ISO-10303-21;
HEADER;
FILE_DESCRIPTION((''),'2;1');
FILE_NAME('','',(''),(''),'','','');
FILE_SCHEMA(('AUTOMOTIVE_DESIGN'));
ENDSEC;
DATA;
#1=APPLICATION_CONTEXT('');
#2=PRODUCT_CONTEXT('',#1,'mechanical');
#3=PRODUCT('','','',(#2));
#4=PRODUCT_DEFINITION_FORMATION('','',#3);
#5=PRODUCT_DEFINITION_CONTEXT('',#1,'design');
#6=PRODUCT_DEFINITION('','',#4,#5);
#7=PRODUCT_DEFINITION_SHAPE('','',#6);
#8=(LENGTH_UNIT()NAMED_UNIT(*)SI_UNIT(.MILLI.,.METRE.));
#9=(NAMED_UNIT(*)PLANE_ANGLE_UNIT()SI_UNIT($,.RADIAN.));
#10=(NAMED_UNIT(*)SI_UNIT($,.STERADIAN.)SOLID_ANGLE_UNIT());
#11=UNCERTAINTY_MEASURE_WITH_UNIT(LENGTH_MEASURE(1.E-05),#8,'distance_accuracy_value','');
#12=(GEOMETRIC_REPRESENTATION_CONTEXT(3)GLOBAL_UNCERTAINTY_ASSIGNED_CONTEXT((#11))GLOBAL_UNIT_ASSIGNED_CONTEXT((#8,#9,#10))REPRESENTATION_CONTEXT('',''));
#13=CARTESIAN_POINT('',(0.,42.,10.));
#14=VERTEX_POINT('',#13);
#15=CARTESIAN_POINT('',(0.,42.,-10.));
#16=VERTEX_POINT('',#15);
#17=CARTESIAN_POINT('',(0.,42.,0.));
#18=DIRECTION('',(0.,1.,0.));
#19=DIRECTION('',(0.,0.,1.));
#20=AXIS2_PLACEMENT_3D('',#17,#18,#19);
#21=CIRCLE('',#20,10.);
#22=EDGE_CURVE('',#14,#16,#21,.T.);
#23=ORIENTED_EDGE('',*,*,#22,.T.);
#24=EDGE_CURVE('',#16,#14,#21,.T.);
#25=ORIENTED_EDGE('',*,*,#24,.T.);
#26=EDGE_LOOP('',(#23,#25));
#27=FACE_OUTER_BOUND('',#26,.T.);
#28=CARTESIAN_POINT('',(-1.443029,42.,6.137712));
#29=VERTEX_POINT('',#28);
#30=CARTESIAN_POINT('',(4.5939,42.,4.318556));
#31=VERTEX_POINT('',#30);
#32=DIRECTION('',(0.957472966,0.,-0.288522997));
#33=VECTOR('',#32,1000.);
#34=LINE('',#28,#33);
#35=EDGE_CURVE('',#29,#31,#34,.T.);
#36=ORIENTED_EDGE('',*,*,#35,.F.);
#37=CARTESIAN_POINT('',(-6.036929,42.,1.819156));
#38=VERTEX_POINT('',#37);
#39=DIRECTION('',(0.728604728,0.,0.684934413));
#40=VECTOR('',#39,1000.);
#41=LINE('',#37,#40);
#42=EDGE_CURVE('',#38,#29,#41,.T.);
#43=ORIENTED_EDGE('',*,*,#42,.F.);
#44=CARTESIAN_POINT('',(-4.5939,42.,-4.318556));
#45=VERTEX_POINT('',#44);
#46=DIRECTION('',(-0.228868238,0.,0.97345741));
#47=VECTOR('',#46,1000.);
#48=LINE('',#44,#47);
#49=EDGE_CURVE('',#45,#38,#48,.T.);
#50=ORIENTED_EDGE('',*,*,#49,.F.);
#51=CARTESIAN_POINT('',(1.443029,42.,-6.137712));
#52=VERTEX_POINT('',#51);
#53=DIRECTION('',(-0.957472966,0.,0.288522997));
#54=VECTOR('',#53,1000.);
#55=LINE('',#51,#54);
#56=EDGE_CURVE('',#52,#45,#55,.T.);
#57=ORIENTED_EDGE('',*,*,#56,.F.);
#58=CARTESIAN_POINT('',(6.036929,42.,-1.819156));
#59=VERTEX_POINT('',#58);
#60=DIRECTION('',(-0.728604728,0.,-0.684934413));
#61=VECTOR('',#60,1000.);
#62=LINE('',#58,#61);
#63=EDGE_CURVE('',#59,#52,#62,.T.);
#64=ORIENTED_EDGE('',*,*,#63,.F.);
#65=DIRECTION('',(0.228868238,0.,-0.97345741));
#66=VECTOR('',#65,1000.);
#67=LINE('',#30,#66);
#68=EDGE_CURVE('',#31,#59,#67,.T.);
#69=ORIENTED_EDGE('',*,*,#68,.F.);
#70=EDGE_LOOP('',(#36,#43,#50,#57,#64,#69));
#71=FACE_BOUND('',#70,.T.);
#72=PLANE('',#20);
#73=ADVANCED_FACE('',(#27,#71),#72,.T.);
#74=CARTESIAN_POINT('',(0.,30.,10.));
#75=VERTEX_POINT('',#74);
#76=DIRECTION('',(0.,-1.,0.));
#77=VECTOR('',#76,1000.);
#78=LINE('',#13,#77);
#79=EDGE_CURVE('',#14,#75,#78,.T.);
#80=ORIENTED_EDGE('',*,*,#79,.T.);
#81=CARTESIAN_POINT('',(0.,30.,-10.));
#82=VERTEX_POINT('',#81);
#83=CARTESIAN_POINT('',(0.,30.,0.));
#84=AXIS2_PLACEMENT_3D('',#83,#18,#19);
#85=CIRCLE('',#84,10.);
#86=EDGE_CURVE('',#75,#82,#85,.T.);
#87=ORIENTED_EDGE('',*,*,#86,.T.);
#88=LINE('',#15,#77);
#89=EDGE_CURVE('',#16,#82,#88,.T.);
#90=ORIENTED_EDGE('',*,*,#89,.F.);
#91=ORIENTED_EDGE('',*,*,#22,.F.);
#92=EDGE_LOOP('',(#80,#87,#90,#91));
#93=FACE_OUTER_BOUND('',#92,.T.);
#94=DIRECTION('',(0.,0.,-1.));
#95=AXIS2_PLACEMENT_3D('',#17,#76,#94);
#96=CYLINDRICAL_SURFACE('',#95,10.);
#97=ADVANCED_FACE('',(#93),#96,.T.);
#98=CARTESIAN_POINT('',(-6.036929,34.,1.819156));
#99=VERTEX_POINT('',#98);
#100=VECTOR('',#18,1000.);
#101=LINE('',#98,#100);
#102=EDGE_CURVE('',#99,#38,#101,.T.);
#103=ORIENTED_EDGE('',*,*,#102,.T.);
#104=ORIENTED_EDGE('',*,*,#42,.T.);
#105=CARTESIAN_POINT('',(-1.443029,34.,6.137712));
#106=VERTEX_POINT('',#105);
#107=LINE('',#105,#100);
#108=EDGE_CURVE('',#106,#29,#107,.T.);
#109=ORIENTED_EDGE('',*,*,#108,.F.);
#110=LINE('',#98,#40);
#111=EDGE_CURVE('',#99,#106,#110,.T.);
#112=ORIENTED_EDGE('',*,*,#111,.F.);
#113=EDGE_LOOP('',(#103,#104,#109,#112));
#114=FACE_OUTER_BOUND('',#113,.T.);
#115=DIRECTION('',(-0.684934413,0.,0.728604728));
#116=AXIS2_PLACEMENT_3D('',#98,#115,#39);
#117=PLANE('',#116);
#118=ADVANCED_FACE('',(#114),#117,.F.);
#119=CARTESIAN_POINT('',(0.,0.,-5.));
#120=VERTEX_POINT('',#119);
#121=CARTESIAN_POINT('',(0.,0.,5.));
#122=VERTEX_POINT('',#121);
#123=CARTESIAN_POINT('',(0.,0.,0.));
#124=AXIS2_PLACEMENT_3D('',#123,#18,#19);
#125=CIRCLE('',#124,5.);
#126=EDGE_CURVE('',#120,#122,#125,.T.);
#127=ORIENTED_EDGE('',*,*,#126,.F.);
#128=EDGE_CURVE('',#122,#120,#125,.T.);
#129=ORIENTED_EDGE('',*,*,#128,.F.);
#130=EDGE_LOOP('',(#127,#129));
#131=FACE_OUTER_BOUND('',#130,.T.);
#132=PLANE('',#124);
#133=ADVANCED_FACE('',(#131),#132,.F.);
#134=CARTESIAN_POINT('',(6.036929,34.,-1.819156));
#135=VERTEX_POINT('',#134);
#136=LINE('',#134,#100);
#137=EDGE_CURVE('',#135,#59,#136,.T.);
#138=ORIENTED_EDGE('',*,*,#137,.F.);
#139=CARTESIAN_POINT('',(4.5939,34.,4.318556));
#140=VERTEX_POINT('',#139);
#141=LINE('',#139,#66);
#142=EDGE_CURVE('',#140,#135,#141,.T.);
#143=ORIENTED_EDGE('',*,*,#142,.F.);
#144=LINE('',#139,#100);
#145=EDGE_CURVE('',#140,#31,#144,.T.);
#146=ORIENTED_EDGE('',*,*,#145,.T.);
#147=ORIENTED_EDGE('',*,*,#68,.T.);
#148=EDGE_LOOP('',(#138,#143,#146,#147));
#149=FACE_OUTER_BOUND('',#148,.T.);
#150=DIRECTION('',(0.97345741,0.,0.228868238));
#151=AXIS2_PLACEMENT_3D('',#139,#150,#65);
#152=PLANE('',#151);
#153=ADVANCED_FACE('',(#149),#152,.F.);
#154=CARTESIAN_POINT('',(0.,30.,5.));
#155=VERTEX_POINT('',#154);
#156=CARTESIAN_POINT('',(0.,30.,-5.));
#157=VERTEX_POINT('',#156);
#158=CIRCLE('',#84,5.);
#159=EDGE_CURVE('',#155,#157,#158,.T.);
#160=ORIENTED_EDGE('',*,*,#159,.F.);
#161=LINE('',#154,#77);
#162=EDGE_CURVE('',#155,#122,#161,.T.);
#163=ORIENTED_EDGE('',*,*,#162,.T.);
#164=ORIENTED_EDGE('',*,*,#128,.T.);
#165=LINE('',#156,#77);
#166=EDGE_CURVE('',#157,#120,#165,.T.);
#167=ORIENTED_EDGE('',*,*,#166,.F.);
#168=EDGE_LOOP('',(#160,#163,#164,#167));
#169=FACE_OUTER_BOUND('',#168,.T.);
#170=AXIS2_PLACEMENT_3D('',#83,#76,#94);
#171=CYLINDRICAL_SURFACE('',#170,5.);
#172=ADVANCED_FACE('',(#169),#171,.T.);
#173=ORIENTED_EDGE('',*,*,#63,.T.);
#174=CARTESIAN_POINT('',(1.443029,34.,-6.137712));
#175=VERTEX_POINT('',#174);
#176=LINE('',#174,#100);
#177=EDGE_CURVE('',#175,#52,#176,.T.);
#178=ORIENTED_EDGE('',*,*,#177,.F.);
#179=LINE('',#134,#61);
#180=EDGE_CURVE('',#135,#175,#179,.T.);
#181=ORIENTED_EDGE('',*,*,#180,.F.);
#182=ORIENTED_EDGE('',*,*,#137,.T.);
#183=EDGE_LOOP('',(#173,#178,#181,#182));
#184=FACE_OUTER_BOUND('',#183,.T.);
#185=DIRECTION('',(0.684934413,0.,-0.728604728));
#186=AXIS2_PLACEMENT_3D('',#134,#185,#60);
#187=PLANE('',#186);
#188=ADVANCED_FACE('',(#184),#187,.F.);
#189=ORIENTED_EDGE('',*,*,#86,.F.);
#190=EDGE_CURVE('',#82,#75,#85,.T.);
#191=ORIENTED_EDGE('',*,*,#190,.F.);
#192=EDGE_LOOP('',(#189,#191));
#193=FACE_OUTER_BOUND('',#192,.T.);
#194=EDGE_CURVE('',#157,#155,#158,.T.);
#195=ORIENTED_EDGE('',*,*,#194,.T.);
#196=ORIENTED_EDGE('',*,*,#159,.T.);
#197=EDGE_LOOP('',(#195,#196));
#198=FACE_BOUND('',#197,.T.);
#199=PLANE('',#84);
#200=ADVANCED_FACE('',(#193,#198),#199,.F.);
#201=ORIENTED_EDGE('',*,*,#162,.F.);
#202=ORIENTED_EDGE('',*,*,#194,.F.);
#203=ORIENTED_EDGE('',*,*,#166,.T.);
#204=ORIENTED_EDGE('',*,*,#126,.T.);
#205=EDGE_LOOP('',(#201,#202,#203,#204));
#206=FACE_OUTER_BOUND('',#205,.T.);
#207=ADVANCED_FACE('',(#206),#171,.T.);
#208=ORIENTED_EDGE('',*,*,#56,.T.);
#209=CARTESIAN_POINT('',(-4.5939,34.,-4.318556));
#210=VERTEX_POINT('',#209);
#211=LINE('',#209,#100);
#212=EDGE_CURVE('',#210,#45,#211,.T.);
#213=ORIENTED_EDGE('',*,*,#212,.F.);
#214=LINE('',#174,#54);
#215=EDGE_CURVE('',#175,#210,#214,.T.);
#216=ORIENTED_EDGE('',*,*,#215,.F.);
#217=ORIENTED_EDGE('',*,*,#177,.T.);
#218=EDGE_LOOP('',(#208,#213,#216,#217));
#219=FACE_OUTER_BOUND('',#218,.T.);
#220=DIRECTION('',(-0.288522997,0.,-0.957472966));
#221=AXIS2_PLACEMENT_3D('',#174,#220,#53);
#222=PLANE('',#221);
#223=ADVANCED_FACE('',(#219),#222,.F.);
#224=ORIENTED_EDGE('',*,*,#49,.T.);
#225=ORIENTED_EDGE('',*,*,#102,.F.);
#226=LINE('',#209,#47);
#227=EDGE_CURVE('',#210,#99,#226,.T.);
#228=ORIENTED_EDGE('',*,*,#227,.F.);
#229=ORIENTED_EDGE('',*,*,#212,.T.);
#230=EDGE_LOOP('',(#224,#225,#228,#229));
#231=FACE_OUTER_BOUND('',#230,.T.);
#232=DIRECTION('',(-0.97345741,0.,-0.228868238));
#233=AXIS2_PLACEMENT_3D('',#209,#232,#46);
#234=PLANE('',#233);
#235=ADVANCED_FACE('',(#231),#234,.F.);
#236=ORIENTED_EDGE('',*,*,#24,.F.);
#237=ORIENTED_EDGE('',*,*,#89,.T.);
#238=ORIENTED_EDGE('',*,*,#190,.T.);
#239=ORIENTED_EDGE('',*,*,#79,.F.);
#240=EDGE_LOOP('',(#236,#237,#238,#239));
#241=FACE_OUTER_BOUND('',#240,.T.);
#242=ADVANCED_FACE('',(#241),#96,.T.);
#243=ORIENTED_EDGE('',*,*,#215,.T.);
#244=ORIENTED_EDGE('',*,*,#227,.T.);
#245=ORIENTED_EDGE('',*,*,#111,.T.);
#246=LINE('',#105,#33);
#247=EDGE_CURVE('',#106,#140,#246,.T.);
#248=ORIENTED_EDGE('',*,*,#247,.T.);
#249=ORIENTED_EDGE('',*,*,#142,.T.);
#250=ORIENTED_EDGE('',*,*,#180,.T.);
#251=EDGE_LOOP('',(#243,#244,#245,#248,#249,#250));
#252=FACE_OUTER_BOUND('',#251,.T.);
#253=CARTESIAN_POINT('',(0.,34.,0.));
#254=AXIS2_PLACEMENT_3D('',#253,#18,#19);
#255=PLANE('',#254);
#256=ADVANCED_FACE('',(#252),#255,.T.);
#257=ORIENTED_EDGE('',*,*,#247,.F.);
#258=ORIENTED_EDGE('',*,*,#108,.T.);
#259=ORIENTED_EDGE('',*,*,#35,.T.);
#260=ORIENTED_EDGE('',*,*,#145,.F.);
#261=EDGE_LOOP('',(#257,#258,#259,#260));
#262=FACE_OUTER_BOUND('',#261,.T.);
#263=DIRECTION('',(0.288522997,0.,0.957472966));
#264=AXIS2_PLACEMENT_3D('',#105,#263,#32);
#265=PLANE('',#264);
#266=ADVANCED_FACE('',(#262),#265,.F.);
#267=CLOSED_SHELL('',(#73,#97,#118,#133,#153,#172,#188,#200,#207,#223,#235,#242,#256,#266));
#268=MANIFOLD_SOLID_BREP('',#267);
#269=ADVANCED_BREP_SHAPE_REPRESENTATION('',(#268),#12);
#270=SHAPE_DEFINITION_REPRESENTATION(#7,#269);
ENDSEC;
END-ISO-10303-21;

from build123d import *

# Parameters (mm, degrees)
SKETCH1_R           = 5
BOSS_EXTRUDE1_DEPTH = 30
SKETCH2_R           = 10
BOSS_EXTRUDE2_DEPTH = 12
CUT_EXTRUDE1_DEPTH  = 8


with BuildPart() as part:
    # Sketch1 → Boss-Extrude1 (new body)
    with BuildSketch(Plane(origin=(0, 0, 0), x_dir=(1, 0, 0), z_dir=(0, 1, 0))):
        with Locations(Location((0, 0, 0), (0, 0, 270))):
            Circle(SKETCH1_R)
    extrude(amount=BOSS_EXTRUDE1_DEPTH)

    # Sketch2 → Boss-Extrude2 (add)
    with BuildSketch(Plane(origin=(0, 30, 0), x_dir=(1, 0, 0), z_dir=(0, 1, 0))):
        with Locations(Location((0, 0, 0), (0, 0, 270))):
            Circle(SKETCH2_R)
    extrude(amount=BOSS_EXTRUDE2_DEPTH)

    # Sketch3 → Cut-Extrude1 (cut)
    with BuildSketch(Plane(origin=(0, 42, 0), x_dir=(1, 0, 0), z_dir=(0, 1, 0))):
        Polygon((4.59389972, -4.318555573), (6.036928694, 1.819156074), (1.443028974, 6.137711647), (-4.59389972, 4.318555573), (-6.036928694, -1.819156074), (-1.443028974, -6.137711647), align=None)
    extrude(amount=-CUT_EXTRUDE1_DEPTH, mode=Mode.SUBTRACT)


solid = part.part
